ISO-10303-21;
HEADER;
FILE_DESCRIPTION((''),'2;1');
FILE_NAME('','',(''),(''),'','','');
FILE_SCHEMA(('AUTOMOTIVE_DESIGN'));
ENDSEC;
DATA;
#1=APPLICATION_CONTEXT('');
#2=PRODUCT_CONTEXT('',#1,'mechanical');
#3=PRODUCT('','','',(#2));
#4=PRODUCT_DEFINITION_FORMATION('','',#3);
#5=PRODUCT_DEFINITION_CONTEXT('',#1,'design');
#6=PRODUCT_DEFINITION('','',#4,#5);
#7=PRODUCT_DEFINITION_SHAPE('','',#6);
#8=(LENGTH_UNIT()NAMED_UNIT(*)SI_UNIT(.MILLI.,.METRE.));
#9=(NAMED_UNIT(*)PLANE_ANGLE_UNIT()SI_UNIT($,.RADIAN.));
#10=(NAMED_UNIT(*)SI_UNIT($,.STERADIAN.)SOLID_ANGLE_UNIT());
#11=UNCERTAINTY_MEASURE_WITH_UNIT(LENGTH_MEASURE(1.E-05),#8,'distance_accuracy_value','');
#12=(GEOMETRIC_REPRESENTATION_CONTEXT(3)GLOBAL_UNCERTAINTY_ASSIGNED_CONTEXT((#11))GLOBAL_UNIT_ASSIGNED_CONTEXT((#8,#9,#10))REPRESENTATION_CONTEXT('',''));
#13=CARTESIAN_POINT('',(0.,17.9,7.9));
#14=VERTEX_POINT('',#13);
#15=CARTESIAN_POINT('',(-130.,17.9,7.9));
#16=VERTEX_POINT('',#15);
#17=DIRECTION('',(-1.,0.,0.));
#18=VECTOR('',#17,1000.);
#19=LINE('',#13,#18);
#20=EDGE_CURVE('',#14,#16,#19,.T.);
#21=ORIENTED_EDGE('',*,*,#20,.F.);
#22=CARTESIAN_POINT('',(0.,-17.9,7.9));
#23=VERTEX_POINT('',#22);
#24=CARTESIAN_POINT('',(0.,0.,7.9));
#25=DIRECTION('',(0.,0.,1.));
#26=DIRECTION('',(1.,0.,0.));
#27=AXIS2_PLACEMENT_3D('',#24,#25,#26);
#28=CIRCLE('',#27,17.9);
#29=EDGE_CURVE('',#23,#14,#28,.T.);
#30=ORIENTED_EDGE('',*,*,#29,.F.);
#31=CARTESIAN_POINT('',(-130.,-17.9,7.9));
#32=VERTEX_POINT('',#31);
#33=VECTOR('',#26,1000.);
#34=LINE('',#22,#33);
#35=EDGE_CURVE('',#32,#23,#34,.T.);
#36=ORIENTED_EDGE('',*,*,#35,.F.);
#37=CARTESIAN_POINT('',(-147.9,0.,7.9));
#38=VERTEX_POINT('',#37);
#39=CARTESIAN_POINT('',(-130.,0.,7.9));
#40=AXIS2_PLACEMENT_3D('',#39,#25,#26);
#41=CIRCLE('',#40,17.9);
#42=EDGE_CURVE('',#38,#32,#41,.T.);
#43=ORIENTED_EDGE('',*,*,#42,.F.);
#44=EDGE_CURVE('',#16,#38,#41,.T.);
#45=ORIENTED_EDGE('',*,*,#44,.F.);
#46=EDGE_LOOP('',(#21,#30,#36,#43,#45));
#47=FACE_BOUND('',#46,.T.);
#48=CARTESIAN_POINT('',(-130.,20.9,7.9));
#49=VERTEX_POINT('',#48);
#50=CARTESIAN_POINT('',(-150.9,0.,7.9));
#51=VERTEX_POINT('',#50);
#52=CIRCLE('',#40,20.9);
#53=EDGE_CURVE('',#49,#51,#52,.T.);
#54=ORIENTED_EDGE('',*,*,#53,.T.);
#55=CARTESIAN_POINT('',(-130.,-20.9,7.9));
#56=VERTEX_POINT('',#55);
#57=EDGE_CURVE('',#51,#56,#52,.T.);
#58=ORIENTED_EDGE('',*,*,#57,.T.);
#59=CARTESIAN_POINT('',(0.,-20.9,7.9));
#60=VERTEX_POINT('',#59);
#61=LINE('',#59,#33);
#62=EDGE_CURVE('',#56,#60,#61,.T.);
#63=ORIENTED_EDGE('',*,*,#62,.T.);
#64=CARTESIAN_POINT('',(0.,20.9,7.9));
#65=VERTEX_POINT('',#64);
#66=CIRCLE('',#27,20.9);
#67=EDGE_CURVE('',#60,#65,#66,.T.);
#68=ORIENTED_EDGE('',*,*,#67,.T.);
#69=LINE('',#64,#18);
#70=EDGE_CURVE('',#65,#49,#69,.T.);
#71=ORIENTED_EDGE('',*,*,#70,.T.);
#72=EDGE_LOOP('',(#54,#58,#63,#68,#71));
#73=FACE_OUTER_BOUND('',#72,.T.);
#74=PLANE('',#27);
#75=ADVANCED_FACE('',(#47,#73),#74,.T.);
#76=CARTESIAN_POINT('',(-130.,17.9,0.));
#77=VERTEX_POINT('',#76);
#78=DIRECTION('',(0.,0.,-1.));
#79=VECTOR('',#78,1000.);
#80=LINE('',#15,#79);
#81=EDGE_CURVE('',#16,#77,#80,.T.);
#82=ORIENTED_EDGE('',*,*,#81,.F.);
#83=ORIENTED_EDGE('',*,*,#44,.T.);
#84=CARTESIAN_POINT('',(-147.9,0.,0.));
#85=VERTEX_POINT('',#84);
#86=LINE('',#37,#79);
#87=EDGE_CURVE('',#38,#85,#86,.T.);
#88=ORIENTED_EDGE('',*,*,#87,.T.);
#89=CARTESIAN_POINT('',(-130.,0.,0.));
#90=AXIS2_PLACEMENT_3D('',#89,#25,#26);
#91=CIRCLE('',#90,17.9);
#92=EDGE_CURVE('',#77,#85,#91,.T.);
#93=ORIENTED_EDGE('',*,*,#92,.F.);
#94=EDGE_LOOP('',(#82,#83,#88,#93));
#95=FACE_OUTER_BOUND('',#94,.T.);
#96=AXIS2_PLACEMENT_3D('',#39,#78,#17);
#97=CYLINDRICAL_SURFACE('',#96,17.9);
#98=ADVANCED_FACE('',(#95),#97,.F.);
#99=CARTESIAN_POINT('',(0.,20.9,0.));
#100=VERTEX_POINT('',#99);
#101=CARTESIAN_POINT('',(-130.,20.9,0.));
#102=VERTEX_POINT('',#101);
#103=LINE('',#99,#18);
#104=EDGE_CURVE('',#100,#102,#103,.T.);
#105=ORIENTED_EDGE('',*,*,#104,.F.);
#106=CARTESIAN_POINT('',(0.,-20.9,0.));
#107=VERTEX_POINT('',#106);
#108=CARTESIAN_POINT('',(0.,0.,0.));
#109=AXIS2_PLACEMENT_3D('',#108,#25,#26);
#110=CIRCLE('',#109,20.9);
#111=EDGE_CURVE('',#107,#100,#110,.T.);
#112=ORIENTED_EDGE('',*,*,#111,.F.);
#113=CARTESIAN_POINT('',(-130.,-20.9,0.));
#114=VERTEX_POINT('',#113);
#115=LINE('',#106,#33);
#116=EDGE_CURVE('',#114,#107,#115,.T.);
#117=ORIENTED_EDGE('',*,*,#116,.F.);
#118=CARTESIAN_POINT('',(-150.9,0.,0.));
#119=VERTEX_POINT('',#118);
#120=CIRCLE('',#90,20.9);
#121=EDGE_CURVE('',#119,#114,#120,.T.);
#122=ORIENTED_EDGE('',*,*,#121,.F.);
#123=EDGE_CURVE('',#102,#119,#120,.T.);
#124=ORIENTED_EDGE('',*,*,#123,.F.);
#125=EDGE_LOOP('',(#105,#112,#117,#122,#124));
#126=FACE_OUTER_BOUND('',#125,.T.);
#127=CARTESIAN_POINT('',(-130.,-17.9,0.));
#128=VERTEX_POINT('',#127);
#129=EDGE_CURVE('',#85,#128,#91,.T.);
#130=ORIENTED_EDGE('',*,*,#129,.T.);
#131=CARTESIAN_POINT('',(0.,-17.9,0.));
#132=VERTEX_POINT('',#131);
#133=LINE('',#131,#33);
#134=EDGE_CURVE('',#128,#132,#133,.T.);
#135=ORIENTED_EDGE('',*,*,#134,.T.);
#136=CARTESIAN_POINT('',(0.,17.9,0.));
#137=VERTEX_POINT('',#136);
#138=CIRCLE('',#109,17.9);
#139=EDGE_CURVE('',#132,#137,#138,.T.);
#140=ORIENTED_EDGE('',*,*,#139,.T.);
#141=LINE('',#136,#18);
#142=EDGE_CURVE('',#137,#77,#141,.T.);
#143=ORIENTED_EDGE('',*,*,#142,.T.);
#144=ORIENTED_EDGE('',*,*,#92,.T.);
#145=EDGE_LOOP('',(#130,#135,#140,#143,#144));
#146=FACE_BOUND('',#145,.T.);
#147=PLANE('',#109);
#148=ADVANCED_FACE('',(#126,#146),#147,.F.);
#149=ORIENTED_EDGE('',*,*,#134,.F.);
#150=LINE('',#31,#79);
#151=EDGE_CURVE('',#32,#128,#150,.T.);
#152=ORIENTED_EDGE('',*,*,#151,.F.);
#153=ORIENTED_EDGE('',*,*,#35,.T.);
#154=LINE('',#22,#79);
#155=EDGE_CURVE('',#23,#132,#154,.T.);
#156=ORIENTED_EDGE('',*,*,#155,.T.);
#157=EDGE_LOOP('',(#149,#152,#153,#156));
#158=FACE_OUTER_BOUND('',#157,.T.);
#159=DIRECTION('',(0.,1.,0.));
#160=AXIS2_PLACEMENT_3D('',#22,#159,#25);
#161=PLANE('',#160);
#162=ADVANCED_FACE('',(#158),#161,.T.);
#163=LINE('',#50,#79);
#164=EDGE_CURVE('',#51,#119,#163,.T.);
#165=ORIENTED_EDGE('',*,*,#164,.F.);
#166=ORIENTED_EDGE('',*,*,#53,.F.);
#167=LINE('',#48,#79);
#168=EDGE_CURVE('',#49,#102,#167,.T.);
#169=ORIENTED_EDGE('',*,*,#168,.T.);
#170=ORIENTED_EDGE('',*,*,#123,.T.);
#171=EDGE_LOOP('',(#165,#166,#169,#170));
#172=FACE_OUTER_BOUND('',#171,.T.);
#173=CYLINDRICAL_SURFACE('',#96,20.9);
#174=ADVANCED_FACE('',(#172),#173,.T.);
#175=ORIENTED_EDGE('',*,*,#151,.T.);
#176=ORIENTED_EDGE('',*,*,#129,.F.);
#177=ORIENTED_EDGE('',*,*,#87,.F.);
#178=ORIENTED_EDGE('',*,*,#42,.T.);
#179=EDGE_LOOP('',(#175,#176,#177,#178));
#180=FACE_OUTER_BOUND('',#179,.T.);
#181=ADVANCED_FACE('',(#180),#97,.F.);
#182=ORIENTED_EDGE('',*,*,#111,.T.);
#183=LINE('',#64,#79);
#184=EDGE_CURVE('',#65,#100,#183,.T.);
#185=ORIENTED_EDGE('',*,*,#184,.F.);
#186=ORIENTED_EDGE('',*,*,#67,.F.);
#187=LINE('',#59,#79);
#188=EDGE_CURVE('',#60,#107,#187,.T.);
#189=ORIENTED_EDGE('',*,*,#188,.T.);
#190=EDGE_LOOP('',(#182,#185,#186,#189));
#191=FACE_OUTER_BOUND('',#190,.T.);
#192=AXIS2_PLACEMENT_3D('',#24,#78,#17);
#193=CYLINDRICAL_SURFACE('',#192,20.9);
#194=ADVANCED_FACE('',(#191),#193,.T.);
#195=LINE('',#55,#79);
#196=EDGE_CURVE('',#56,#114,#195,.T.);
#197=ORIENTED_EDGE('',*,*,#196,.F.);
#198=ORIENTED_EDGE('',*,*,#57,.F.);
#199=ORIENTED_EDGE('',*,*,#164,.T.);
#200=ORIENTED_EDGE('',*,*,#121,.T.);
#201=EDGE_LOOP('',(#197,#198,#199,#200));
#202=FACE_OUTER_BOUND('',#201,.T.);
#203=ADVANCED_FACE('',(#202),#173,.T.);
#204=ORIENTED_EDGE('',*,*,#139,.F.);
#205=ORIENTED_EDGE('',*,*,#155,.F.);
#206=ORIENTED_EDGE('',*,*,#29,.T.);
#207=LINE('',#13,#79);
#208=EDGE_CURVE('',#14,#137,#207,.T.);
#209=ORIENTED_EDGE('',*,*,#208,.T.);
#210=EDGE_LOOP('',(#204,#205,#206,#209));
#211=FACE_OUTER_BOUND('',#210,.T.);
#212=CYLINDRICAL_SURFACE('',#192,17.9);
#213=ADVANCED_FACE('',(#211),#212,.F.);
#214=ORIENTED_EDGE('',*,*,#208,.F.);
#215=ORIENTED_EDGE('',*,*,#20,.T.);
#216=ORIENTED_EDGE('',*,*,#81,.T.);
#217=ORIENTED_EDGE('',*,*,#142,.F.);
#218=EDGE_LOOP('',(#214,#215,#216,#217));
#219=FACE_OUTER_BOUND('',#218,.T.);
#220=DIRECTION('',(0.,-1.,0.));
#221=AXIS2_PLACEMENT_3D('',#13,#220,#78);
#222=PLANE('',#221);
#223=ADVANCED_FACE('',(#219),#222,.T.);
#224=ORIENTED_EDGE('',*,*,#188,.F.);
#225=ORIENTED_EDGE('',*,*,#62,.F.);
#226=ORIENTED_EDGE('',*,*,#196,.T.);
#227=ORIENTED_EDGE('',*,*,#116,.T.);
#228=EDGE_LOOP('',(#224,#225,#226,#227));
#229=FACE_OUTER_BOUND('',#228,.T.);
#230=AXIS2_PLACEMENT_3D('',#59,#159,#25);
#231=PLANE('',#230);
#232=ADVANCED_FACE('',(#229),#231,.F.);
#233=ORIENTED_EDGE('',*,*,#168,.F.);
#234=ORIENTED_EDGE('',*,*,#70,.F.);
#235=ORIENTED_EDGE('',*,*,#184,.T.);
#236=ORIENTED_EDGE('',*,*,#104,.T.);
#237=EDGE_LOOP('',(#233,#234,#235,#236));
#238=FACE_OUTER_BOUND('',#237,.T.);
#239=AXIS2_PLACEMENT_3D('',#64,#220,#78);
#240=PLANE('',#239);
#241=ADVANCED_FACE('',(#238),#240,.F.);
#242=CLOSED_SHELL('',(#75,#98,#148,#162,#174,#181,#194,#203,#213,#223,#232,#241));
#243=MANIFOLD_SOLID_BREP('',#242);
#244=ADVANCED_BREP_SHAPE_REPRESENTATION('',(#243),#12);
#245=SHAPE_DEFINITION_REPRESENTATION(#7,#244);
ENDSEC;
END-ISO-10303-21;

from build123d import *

# Parameters (mm, degrees)
BOSS_EXTRUDE1_DEPTH = 7.9
SHELL1_T            = -3


with BuildPart() as part:
    # Sketch2 → Boss-Extrude1 (new body)
    with BuildSketch(Plane.XY):
        with BuildLine():
            Line((0, 20.9), (-130, 20.9))
            ThreePointArc((-130, 20.9), (-150.9, 0), (-130, -20.9))
            Line((-130, -20.9), (0, -20.9))
            ThreePointArc((0, -20.9), (20.9, 0), (0, 20.9))
        make_face()
    extrude(amount=BOSS_EXTRUDE1_DEPTH)

    # Shell1
    shell1_openings = [part.faces().sort_by_distance(p)[0] for p in [
        (-65, 0, 7.9),
        (-65, 0, 0),
    ]]
    offset(amount=SHELL1_T, openings=shell1_openings, kind=Kind.INTERSECTION)


solid = part.part
